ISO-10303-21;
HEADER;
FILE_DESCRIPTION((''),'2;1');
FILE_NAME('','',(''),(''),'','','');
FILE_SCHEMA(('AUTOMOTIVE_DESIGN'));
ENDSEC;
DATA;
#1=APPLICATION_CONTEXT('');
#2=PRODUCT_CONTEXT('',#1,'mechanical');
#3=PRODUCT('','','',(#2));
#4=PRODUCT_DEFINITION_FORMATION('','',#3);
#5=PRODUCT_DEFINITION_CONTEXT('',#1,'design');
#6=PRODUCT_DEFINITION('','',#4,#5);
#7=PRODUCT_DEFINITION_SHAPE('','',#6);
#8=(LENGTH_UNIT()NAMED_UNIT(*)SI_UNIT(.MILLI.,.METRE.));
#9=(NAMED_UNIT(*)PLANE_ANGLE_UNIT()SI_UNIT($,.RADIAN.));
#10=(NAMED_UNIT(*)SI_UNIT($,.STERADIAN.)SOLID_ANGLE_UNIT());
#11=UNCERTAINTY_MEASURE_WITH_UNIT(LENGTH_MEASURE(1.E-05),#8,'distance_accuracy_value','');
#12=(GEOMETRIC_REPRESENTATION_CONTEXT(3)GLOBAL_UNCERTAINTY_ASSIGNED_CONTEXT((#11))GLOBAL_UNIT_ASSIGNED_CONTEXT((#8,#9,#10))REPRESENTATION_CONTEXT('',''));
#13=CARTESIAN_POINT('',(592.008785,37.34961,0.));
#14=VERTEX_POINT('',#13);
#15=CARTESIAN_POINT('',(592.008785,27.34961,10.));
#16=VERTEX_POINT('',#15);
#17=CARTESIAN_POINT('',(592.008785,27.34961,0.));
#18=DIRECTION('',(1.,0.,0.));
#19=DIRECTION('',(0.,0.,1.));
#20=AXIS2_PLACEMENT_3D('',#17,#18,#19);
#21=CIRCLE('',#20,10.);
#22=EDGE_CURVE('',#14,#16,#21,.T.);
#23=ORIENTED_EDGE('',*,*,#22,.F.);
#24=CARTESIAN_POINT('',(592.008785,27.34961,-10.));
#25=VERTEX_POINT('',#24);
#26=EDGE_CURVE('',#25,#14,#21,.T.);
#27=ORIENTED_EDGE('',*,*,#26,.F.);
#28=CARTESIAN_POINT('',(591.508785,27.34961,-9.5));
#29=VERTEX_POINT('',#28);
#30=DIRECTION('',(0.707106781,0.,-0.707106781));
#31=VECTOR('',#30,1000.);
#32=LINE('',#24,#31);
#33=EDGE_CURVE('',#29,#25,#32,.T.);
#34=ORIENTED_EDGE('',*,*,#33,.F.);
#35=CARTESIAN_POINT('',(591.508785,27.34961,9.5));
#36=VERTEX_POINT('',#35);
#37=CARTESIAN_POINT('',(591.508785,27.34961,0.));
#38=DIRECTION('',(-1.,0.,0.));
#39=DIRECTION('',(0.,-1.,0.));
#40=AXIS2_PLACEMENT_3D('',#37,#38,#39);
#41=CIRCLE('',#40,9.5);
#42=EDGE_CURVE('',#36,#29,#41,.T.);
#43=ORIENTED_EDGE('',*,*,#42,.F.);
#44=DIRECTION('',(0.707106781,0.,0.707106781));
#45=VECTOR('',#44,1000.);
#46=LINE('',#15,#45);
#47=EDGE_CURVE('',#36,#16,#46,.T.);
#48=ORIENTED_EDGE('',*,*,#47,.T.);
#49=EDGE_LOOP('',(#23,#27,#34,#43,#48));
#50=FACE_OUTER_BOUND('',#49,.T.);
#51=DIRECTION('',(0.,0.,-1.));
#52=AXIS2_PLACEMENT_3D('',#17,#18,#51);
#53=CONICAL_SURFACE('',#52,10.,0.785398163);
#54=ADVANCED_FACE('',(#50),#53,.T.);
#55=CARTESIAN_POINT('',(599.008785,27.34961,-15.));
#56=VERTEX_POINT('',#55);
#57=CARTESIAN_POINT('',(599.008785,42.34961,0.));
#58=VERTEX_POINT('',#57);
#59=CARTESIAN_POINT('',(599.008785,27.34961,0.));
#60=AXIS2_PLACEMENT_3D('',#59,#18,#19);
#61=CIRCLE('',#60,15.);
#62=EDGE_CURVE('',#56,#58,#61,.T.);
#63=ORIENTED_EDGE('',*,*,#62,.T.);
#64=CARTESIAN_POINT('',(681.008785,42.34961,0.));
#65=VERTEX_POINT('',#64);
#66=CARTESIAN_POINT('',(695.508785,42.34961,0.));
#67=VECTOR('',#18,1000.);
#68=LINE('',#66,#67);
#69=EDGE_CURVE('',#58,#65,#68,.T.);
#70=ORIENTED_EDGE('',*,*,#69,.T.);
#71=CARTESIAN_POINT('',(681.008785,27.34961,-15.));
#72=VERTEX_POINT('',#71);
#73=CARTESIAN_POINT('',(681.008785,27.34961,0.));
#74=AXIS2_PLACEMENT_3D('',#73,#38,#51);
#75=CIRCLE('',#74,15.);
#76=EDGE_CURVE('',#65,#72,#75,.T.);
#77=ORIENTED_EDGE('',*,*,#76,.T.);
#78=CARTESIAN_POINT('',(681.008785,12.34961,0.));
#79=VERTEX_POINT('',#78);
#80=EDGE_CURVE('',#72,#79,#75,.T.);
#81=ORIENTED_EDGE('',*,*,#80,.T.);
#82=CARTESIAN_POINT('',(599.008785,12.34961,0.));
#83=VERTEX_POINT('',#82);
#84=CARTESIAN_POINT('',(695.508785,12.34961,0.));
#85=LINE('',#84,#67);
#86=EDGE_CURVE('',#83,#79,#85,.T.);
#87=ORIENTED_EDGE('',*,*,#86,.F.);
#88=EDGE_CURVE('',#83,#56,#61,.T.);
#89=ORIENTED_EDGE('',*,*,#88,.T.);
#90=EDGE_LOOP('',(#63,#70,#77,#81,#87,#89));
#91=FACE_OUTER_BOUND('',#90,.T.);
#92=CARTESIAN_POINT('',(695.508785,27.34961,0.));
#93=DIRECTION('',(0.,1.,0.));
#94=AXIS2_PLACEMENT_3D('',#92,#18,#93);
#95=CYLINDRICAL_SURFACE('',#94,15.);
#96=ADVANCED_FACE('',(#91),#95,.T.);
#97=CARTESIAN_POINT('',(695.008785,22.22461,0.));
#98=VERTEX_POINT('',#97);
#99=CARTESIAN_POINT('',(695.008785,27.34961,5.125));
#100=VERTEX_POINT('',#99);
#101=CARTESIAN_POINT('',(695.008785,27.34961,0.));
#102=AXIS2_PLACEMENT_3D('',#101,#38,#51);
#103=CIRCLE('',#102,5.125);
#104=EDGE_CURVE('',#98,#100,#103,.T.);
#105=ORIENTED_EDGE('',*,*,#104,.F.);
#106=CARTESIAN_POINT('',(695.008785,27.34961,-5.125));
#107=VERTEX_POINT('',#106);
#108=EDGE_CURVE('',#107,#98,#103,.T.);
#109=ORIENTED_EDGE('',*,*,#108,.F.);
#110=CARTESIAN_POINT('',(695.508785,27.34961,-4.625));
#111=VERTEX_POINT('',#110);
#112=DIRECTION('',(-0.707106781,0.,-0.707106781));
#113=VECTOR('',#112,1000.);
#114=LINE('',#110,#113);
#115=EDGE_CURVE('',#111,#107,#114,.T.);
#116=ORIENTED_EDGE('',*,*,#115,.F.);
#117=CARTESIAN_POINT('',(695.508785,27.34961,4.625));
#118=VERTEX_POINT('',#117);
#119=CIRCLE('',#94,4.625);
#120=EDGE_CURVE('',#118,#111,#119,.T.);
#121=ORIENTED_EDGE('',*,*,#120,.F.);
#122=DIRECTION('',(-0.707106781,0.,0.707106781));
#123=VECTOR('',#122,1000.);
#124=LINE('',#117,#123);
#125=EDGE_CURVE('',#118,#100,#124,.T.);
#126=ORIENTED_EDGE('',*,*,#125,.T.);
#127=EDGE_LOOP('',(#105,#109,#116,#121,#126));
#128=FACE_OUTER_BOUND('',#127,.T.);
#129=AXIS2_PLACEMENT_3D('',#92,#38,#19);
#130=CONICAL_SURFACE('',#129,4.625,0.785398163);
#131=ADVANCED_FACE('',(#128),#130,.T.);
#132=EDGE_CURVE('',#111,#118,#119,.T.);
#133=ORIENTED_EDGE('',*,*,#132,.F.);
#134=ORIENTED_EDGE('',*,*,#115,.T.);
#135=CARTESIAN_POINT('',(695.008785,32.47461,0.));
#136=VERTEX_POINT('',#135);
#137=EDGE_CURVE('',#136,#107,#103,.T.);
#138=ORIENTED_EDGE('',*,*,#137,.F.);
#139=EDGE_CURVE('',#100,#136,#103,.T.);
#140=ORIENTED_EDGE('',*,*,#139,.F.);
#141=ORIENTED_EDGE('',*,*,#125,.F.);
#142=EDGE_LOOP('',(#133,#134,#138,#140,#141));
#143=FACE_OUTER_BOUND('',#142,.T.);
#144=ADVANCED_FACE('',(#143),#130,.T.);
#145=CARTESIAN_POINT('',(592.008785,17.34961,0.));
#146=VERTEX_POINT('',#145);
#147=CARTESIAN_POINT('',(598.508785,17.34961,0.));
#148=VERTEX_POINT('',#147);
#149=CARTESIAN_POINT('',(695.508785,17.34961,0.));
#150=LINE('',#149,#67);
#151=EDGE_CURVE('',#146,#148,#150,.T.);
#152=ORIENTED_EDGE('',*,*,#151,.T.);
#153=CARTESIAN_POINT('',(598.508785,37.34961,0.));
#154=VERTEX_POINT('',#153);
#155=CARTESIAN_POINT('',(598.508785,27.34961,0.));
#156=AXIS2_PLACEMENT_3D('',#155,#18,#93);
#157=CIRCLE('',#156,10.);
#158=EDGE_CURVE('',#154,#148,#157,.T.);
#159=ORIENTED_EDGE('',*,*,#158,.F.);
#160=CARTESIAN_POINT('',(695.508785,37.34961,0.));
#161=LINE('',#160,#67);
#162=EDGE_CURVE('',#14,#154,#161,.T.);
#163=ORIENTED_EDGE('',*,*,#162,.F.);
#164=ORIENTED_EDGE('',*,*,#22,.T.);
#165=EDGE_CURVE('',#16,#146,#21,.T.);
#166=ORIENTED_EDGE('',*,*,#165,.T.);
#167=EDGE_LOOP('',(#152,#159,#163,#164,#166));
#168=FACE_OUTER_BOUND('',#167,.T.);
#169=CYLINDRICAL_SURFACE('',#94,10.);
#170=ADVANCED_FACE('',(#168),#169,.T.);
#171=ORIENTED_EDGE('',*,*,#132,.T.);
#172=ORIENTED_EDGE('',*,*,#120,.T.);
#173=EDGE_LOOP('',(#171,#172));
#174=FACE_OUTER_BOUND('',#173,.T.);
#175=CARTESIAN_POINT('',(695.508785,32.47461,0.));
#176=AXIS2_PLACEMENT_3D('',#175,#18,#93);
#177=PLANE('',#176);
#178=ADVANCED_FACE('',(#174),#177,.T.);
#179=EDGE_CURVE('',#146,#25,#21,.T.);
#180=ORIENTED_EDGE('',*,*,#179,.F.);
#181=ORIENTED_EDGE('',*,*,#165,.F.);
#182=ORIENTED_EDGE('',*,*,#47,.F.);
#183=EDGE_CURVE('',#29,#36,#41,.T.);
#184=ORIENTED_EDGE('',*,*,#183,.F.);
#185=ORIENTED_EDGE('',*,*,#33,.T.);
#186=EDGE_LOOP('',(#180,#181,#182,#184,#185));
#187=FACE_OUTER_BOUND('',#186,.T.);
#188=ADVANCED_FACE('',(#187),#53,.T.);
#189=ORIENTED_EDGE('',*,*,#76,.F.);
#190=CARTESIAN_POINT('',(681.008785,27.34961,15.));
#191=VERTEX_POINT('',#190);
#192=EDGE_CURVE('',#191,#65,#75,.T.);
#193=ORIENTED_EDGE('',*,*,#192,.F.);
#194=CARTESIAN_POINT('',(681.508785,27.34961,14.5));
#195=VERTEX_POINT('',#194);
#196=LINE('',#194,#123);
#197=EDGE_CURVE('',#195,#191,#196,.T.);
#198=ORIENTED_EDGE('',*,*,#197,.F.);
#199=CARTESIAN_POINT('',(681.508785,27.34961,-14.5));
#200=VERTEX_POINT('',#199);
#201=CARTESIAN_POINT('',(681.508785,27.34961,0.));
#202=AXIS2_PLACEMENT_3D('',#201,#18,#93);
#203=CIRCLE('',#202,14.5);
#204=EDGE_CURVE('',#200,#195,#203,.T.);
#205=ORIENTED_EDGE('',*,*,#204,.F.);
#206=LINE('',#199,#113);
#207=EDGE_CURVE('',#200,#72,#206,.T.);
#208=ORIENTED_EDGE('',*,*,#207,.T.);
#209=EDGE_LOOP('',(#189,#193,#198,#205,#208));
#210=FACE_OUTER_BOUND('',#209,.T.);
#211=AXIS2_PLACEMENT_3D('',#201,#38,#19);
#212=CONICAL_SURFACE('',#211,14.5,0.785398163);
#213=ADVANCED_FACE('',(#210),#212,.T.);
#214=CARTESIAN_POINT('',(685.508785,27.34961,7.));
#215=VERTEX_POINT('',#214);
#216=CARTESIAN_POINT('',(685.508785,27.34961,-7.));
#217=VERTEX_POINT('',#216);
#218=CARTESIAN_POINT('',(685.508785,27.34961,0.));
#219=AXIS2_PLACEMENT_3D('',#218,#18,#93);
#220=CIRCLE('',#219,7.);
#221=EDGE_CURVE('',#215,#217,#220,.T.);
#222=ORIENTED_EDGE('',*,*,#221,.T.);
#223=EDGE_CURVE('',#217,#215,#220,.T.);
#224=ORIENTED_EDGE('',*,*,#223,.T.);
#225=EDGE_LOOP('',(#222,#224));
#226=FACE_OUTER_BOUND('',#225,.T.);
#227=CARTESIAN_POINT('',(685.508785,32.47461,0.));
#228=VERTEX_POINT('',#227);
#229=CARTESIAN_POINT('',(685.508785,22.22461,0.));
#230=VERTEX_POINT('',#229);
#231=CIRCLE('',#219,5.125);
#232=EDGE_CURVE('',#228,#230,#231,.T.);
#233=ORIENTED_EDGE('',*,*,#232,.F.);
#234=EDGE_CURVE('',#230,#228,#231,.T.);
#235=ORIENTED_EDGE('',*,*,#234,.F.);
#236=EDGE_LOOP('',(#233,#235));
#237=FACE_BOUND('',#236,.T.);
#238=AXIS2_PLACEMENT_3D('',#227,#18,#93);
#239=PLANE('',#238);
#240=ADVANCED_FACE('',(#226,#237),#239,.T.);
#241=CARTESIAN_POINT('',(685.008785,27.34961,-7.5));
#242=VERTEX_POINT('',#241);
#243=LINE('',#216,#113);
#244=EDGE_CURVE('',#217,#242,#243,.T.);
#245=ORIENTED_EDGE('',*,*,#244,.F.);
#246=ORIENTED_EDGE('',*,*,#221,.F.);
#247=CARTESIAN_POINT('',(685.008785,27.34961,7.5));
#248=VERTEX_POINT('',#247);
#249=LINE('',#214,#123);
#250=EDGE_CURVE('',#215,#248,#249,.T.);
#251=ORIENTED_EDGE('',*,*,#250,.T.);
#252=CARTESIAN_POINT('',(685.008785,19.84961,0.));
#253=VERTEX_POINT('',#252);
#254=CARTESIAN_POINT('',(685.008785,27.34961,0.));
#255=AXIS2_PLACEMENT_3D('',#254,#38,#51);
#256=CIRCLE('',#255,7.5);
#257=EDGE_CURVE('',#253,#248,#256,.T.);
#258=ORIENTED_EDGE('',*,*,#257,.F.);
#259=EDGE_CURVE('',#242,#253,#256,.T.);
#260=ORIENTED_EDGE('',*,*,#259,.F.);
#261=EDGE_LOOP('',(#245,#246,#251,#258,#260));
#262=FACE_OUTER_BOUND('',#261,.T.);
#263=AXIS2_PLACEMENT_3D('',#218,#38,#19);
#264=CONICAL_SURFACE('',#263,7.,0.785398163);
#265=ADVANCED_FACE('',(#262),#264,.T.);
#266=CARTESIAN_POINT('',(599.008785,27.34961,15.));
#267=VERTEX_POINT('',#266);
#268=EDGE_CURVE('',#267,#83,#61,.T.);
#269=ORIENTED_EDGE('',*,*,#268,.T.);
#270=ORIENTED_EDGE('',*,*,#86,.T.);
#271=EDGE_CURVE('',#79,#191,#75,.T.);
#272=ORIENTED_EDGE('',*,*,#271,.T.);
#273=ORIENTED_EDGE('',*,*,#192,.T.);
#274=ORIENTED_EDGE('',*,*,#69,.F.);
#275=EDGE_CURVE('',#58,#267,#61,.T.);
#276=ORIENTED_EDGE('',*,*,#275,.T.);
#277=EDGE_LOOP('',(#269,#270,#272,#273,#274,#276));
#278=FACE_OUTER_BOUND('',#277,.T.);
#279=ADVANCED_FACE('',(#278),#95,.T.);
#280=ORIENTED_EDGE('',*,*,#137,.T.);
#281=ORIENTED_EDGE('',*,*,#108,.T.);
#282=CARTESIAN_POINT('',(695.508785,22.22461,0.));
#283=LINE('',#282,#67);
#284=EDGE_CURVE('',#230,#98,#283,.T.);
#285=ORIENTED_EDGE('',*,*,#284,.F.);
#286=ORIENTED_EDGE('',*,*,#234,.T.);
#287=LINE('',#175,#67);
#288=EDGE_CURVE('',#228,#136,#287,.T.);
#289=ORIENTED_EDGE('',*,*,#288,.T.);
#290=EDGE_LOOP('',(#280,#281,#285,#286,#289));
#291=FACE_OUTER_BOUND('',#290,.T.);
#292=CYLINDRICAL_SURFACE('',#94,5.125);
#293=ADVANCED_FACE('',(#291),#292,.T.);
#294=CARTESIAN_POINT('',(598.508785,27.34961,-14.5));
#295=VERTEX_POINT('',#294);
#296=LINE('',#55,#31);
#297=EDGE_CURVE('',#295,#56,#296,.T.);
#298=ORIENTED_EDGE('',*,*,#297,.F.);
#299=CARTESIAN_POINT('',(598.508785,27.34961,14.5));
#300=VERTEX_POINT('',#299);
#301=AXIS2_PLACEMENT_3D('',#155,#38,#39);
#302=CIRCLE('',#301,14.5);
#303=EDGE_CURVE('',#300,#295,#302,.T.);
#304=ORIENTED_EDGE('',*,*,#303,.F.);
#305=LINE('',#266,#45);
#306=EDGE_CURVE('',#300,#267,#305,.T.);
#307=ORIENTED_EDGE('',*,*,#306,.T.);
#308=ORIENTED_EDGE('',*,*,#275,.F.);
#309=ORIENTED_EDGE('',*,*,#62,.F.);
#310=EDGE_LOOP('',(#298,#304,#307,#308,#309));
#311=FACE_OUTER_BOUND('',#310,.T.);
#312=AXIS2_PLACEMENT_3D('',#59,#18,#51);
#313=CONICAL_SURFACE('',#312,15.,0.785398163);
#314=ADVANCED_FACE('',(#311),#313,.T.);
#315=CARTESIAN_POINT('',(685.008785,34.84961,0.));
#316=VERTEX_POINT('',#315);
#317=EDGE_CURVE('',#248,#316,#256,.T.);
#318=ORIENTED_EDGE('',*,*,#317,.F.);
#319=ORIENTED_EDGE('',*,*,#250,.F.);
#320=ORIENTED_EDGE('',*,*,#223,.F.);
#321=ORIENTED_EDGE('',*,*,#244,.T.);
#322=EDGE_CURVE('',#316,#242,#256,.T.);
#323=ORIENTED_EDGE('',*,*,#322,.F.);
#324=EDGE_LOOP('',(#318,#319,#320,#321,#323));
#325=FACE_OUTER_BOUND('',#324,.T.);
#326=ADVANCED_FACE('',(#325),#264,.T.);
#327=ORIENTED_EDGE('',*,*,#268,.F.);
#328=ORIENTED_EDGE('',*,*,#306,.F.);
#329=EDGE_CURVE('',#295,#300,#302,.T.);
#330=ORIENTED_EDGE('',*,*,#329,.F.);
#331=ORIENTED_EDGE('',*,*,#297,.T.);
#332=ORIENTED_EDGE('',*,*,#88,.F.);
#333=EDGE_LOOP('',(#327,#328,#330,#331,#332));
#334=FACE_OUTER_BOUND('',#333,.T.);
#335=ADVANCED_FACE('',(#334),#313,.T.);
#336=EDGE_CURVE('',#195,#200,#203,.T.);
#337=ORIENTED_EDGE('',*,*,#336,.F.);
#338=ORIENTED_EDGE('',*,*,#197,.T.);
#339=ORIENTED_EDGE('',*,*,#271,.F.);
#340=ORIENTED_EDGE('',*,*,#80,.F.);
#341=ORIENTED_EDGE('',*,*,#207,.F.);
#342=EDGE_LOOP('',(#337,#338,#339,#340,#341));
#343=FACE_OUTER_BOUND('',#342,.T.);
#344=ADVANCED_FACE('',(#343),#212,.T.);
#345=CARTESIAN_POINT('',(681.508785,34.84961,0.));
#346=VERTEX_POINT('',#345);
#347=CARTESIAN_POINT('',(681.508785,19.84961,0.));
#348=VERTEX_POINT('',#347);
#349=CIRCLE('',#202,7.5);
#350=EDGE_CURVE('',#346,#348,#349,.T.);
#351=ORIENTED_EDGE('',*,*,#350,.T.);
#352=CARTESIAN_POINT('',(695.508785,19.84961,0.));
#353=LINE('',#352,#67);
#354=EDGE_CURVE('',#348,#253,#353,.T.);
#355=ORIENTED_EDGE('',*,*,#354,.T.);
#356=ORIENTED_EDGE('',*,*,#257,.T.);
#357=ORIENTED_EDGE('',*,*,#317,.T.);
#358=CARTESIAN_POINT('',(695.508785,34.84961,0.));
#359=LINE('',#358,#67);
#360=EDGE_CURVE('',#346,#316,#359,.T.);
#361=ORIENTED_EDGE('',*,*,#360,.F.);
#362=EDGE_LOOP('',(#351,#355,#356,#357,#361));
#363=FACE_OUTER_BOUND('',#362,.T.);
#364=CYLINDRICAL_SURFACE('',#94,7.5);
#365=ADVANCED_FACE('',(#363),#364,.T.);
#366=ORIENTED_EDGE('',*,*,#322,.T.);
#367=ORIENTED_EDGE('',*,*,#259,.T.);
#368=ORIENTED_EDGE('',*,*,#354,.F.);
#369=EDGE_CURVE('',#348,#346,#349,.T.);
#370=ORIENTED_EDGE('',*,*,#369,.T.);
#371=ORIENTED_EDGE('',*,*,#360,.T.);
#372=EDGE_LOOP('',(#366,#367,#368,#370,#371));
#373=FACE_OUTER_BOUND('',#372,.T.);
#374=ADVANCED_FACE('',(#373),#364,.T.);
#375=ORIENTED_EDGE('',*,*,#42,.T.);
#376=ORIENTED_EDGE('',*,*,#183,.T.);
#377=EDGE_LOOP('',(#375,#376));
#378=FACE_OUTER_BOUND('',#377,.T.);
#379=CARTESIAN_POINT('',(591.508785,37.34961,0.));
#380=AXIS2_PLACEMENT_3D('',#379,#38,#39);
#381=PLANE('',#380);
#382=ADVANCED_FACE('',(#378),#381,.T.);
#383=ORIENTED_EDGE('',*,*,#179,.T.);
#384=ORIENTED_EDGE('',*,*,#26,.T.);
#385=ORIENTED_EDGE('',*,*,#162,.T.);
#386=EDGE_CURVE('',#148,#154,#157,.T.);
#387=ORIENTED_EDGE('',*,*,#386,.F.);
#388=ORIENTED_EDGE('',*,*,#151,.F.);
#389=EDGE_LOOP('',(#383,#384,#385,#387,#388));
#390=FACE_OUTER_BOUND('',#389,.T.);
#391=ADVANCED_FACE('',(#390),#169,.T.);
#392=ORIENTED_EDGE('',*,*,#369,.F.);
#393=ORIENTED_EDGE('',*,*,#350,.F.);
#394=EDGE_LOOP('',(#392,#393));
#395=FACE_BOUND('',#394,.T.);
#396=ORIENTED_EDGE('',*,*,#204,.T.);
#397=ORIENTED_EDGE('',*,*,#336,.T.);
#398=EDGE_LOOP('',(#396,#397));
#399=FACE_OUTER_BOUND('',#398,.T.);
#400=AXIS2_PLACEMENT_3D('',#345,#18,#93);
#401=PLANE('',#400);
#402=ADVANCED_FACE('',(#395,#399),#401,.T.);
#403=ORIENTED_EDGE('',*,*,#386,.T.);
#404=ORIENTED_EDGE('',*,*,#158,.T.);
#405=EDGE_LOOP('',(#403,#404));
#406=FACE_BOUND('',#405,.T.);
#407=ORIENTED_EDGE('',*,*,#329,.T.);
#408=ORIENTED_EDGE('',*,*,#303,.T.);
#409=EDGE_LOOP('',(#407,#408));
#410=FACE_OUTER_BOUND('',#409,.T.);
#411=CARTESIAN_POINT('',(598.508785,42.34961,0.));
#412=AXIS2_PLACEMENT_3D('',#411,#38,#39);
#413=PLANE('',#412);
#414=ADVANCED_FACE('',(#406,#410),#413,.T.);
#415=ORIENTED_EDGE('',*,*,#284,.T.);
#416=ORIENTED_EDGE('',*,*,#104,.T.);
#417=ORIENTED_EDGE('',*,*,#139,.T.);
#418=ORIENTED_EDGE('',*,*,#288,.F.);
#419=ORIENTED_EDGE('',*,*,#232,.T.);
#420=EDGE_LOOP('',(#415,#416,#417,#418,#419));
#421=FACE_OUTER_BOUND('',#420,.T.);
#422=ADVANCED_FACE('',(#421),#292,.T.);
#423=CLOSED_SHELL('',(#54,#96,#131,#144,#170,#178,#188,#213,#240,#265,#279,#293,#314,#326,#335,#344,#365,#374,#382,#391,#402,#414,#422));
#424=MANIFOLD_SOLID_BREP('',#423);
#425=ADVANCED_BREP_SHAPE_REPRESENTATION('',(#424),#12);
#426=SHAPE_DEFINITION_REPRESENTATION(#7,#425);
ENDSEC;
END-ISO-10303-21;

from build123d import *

# Parameters (mm, degrees)
CHAMFER1_SIZE = 0.5


with BuildPart() as part:
    # Sketch1 → Revolve1 (revolve)
    with BuildSketch(Plane.XY):
        Polygon((695.508784709, 32.474610335), (685.508784709, 32.474610335), (685.508784709, 34.849610335), (681.508784709, 34.849610335), (681.508784709, 42.349610335), (598.508784709, 42.349610335), (598.508784709, 37.349610335), (591.508784709, 37.349610335), (591.508784709, 27.349610335), (695.508784709, 27.349610335), align=None)
    revolve(axis=Axis((695.508784709, 27.349610335, 0), (-1, 0, 0)))

    # Chamfer1
    chamfer1_edges = [part.edges().sort_by_distance(p)[0] for p in [
        (598.508784709, 12.349610335, 0),
        (591.508784709, 17.349610335, 0),
        (695.508784709, 22.224610335, 0),
        (685.508784709, 19.849610335, 0),
        (681.508784709, 12.349610335, 0),
    ]]
    chamfer(chamfer1_edges, length=CHAMFER1_SIZE)


solid = part.part
